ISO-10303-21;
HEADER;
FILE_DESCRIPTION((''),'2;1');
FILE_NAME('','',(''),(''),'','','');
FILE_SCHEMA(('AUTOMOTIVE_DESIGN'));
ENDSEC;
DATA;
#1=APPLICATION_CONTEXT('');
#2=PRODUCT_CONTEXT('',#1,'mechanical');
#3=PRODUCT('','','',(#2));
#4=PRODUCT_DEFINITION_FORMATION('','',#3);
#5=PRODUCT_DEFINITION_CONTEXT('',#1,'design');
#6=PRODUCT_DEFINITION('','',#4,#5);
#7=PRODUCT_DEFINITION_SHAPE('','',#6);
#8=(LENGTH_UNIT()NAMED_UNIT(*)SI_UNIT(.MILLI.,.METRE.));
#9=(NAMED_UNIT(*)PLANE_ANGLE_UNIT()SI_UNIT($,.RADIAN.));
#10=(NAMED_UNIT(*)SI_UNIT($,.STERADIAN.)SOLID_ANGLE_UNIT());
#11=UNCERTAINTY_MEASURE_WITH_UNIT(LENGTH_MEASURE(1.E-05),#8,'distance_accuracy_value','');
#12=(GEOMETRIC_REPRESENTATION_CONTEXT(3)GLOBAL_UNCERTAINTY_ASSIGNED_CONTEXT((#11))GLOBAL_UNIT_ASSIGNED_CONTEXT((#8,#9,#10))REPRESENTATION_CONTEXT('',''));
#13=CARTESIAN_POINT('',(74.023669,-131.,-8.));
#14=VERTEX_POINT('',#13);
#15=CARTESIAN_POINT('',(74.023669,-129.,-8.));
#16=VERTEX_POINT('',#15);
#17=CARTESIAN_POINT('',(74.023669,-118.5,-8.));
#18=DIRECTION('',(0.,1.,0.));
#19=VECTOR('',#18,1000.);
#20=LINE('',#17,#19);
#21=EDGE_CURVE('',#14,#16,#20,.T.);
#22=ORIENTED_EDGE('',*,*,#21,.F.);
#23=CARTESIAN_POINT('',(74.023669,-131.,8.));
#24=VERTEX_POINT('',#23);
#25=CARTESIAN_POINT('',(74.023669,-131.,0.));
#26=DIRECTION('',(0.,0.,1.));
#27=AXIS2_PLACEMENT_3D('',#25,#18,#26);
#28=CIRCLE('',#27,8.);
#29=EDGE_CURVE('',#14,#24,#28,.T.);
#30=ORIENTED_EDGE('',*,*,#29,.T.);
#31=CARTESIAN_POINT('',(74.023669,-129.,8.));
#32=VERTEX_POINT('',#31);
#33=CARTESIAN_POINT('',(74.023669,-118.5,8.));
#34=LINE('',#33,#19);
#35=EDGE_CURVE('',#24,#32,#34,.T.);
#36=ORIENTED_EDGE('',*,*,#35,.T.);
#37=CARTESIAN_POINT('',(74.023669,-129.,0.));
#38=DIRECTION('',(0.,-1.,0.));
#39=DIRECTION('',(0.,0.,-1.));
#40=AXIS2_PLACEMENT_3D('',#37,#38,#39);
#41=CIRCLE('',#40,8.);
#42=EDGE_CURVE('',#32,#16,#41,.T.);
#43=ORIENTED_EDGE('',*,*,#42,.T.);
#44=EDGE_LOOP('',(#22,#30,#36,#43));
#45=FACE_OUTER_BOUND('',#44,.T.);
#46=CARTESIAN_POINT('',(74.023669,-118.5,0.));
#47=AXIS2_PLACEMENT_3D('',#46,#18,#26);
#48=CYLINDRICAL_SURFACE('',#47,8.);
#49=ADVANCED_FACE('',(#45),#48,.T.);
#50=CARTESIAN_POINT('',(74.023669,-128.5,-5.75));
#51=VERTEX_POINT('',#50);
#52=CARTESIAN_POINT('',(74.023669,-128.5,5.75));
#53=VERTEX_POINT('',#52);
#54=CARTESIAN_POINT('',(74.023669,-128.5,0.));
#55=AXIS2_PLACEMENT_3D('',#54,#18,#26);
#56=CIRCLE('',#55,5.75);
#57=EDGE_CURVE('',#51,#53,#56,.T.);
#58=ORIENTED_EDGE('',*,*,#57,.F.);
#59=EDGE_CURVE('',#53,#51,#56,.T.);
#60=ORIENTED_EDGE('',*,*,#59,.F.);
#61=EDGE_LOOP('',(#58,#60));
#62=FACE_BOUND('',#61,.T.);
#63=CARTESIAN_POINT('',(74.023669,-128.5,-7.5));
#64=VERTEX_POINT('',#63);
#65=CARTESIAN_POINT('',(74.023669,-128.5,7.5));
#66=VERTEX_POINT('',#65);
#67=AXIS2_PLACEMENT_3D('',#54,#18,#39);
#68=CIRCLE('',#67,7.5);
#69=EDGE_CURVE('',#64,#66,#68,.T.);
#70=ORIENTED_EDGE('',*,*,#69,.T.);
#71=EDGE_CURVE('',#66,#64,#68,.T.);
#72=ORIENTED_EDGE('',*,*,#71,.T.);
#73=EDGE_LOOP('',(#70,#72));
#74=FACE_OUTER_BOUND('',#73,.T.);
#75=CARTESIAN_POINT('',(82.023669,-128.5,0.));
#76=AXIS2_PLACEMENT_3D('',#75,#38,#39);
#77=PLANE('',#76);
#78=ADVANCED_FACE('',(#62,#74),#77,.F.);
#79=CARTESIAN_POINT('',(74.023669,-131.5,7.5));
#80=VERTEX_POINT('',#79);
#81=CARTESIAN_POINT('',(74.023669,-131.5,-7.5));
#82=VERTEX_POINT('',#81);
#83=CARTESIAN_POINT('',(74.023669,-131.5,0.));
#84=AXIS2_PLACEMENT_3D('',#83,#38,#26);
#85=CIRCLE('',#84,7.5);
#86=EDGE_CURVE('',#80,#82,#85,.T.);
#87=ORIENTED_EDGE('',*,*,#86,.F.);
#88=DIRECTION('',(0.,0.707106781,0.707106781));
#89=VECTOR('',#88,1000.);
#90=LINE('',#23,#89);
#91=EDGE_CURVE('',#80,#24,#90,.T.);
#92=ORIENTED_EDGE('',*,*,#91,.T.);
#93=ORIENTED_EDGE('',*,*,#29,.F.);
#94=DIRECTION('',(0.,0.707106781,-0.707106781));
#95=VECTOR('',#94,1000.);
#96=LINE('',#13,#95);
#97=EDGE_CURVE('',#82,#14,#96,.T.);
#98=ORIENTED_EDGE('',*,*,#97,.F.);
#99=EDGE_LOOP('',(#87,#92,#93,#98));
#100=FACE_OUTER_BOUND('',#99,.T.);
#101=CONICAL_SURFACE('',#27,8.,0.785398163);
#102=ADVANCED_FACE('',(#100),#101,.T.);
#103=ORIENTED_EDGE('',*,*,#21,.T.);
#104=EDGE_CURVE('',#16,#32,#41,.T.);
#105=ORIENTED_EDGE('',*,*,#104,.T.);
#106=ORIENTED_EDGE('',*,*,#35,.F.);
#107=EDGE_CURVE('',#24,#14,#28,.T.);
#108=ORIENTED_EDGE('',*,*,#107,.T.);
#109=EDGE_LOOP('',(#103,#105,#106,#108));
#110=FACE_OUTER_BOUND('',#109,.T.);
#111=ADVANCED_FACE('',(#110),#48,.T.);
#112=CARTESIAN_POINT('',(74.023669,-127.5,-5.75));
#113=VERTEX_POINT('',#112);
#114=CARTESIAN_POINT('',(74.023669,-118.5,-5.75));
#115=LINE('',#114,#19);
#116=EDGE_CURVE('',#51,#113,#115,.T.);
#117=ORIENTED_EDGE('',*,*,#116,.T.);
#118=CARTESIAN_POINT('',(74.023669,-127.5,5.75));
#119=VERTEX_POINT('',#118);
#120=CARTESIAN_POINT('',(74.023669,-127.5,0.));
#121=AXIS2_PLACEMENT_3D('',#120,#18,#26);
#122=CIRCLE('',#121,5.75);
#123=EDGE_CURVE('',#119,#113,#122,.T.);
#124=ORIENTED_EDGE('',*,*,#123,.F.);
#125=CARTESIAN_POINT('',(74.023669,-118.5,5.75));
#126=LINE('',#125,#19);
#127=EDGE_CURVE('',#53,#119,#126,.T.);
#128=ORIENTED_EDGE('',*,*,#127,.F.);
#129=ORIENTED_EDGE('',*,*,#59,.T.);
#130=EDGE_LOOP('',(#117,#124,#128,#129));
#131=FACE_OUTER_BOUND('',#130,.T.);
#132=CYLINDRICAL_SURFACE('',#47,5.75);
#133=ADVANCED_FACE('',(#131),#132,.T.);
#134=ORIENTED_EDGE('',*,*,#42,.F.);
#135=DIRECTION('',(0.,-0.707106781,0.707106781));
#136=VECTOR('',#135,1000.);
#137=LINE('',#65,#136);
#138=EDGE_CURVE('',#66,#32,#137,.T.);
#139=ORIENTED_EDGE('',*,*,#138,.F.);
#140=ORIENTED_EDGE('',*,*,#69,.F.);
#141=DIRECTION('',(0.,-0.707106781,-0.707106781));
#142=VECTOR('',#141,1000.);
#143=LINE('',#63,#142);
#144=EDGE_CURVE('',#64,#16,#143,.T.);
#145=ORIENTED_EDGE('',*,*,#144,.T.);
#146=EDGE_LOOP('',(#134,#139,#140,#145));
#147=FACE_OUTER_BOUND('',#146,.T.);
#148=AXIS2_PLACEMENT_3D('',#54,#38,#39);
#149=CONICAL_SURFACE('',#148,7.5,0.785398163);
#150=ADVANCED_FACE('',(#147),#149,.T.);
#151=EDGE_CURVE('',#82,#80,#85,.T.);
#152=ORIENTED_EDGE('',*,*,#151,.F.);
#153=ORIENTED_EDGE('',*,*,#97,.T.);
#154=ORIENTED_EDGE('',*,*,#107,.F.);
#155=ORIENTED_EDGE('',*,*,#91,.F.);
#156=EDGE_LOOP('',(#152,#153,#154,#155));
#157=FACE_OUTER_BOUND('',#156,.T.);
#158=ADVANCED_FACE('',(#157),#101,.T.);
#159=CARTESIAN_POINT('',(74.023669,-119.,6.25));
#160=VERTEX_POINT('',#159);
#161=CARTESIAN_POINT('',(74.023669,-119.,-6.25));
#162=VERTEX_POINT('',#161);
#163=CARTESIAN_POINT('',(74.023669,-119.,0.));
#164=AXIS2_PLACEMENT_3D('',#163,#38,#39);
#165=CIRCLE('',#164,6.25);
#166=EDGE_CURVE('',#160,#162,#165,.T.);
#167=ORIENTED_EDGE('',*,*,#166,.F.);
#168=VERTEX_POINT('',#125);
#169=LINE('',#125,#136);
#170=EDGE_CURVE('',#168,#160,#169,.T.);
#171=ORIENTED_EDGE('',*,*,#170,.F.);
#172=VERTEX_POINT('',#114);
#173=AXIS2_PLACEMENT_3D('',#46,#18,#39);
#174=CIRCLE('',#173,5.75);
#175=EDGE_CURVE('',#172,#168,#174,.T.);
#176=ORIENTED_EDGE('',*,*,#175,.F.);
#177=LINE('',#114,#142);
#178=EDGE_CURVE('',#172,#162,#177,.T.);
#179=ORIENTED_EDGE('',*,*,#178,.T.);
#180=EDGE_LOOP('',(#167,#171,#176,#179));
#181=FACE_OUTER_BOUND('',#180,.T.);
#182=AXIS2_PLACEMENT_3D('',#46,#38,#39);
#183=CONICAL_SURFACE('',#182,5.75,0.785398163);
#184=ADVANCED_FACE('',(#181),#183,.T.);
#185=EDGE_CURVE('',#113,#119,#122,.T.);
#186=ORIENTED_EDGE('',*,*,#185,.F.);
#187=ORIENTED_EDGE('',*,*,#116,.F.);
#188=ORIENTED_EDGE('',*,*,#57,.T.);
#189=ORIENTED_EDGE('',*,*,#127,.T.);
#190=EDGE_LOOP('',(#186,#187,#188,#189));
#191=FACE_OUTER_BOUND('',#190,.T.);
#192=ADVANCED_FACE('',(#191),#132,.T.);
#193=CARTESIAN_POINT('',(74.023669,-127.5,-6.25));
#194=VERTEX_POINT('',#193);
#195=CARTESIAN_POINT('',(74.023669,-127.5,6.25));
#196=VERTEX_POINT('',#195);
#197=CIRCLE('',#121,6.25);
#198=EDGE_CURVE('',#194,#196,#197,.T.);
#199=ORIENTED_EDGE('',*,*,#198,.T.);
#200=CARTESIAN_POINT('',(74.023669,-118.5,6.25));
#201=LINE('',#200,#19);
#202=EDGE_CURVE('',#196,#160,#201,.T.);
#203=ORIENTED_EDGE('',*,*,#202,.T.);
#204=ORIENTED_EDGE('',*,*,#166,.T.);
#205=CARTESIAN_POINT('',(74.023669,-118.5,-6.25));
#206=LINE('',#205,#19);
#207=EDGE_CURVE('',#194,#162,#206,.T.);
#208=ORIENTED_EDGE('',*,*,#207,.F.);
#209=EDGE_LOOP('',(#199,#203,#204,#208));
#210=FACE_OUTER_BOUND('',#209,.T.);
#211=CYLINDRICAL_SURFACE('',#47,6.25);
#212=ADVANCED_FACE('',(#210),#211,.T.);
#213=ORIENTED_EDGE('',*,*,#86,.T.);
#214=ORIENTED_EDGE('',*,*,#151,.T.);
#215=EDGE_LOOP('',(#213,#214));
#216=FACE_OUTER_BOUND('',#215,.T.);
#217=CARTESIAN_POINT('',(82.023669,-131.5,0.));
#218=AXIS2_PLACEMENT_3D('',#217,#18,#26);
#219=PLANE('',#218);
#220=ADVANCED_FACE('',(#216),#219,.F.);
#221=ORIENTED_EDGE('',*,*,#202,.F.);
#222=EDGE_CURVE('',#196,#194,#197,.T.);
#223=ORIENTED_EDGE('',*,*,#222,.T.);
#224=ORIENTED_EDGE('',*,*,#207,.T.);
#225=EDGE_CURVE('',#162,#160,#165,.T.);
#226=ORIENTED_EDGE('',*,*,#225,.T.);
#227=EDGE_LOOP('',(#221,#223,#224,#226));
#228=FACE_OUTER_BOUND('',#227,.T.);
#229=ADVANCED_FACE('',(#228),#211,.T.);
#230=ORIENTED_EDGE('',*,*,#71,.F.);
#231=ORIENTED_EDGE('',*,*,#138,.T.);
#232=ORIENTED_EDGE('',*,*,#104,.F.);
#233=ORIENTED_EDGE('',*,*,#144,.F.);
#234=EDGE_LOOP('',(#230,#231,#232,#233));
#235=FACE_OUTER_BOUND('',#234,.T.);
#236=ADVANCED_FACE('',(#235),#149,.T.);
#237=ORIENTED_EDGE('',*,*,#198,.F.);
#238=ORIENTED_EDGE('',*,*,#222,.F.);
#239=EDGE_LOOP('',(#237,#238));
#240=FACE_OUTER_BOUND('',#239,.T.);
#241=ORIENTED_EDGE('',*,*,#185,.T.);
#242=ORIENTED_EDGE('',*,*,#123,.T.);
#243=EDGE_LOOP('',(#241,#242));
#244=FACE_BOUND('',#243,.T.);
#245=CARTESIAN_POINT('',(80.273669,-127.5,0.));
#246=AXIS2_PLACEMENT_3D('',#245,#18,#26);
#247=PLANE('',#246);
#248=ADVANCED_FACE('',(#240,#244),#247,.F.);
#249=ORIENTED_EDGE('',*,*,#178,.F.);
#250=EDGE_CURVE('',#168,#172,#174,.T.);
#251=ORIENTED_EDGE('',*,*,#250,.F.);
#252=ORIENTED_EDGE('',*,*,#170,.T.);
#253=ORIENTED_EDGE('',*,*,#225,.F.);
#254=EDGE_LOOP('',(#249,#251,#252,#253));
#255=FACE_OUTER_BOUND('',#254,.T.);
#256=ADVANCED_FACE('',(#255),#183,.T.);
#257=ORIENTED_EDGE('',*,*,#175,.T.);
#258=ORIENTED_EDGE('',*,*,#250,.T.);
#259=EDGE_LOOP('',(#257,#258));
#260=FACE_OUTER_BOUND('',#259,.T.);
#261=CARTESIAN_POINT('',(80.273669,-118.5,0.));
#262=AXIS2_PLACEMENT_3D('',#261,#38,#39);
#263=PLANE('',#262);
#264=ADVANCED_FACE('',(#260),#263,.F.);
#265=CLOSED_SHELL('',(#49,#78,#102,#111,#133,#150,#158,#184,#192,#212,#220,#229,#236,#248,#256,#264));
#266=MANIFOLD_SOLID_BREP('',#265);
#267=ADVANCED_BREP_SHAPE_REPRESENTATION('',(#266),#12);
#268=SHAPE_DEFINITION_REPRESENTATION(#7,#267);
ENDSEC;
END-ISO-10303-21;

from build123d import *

# Parameters (mm, degrees)
CHAMFER1_SIZE = 0.5


with BuildPart() as part:
    # Sketch1 → Revolve1 (revolve)
    with BuildSketch(Plane.XY, mode=Mode.PRIVATE) as revolve1_sk:
        Polygon((74.023669398, -131.5), (74.023669398, -118.5), (80.273669398, -118.5), (80.273669398, -127.5), (79.773669398, -127.5), (79.773669398, -128.5), (82.023669398, -128.5), (82.023669398, -131.5), align=None)
    revolve(revolve1_sk.sketch.rotate(Axis((74.023669398, -118.5, 0), (0, -1, 0)), 90), axis=Axis((74.023669398, -118.5, 0), (0, -1, 0)))

    # Chamfer1
    chamfer1_edges = [part.edges().sort_by_distance(p)[0] for p in [
        (74.023669398, -131.5, -8),
        (74.023669398, -128.5, -8),
        (74.023669398, -118.5, -6.25),
    ]]
    chamfer(chamfer1_edges, length=CHAMFER1_SIZE)


solid = part.part
